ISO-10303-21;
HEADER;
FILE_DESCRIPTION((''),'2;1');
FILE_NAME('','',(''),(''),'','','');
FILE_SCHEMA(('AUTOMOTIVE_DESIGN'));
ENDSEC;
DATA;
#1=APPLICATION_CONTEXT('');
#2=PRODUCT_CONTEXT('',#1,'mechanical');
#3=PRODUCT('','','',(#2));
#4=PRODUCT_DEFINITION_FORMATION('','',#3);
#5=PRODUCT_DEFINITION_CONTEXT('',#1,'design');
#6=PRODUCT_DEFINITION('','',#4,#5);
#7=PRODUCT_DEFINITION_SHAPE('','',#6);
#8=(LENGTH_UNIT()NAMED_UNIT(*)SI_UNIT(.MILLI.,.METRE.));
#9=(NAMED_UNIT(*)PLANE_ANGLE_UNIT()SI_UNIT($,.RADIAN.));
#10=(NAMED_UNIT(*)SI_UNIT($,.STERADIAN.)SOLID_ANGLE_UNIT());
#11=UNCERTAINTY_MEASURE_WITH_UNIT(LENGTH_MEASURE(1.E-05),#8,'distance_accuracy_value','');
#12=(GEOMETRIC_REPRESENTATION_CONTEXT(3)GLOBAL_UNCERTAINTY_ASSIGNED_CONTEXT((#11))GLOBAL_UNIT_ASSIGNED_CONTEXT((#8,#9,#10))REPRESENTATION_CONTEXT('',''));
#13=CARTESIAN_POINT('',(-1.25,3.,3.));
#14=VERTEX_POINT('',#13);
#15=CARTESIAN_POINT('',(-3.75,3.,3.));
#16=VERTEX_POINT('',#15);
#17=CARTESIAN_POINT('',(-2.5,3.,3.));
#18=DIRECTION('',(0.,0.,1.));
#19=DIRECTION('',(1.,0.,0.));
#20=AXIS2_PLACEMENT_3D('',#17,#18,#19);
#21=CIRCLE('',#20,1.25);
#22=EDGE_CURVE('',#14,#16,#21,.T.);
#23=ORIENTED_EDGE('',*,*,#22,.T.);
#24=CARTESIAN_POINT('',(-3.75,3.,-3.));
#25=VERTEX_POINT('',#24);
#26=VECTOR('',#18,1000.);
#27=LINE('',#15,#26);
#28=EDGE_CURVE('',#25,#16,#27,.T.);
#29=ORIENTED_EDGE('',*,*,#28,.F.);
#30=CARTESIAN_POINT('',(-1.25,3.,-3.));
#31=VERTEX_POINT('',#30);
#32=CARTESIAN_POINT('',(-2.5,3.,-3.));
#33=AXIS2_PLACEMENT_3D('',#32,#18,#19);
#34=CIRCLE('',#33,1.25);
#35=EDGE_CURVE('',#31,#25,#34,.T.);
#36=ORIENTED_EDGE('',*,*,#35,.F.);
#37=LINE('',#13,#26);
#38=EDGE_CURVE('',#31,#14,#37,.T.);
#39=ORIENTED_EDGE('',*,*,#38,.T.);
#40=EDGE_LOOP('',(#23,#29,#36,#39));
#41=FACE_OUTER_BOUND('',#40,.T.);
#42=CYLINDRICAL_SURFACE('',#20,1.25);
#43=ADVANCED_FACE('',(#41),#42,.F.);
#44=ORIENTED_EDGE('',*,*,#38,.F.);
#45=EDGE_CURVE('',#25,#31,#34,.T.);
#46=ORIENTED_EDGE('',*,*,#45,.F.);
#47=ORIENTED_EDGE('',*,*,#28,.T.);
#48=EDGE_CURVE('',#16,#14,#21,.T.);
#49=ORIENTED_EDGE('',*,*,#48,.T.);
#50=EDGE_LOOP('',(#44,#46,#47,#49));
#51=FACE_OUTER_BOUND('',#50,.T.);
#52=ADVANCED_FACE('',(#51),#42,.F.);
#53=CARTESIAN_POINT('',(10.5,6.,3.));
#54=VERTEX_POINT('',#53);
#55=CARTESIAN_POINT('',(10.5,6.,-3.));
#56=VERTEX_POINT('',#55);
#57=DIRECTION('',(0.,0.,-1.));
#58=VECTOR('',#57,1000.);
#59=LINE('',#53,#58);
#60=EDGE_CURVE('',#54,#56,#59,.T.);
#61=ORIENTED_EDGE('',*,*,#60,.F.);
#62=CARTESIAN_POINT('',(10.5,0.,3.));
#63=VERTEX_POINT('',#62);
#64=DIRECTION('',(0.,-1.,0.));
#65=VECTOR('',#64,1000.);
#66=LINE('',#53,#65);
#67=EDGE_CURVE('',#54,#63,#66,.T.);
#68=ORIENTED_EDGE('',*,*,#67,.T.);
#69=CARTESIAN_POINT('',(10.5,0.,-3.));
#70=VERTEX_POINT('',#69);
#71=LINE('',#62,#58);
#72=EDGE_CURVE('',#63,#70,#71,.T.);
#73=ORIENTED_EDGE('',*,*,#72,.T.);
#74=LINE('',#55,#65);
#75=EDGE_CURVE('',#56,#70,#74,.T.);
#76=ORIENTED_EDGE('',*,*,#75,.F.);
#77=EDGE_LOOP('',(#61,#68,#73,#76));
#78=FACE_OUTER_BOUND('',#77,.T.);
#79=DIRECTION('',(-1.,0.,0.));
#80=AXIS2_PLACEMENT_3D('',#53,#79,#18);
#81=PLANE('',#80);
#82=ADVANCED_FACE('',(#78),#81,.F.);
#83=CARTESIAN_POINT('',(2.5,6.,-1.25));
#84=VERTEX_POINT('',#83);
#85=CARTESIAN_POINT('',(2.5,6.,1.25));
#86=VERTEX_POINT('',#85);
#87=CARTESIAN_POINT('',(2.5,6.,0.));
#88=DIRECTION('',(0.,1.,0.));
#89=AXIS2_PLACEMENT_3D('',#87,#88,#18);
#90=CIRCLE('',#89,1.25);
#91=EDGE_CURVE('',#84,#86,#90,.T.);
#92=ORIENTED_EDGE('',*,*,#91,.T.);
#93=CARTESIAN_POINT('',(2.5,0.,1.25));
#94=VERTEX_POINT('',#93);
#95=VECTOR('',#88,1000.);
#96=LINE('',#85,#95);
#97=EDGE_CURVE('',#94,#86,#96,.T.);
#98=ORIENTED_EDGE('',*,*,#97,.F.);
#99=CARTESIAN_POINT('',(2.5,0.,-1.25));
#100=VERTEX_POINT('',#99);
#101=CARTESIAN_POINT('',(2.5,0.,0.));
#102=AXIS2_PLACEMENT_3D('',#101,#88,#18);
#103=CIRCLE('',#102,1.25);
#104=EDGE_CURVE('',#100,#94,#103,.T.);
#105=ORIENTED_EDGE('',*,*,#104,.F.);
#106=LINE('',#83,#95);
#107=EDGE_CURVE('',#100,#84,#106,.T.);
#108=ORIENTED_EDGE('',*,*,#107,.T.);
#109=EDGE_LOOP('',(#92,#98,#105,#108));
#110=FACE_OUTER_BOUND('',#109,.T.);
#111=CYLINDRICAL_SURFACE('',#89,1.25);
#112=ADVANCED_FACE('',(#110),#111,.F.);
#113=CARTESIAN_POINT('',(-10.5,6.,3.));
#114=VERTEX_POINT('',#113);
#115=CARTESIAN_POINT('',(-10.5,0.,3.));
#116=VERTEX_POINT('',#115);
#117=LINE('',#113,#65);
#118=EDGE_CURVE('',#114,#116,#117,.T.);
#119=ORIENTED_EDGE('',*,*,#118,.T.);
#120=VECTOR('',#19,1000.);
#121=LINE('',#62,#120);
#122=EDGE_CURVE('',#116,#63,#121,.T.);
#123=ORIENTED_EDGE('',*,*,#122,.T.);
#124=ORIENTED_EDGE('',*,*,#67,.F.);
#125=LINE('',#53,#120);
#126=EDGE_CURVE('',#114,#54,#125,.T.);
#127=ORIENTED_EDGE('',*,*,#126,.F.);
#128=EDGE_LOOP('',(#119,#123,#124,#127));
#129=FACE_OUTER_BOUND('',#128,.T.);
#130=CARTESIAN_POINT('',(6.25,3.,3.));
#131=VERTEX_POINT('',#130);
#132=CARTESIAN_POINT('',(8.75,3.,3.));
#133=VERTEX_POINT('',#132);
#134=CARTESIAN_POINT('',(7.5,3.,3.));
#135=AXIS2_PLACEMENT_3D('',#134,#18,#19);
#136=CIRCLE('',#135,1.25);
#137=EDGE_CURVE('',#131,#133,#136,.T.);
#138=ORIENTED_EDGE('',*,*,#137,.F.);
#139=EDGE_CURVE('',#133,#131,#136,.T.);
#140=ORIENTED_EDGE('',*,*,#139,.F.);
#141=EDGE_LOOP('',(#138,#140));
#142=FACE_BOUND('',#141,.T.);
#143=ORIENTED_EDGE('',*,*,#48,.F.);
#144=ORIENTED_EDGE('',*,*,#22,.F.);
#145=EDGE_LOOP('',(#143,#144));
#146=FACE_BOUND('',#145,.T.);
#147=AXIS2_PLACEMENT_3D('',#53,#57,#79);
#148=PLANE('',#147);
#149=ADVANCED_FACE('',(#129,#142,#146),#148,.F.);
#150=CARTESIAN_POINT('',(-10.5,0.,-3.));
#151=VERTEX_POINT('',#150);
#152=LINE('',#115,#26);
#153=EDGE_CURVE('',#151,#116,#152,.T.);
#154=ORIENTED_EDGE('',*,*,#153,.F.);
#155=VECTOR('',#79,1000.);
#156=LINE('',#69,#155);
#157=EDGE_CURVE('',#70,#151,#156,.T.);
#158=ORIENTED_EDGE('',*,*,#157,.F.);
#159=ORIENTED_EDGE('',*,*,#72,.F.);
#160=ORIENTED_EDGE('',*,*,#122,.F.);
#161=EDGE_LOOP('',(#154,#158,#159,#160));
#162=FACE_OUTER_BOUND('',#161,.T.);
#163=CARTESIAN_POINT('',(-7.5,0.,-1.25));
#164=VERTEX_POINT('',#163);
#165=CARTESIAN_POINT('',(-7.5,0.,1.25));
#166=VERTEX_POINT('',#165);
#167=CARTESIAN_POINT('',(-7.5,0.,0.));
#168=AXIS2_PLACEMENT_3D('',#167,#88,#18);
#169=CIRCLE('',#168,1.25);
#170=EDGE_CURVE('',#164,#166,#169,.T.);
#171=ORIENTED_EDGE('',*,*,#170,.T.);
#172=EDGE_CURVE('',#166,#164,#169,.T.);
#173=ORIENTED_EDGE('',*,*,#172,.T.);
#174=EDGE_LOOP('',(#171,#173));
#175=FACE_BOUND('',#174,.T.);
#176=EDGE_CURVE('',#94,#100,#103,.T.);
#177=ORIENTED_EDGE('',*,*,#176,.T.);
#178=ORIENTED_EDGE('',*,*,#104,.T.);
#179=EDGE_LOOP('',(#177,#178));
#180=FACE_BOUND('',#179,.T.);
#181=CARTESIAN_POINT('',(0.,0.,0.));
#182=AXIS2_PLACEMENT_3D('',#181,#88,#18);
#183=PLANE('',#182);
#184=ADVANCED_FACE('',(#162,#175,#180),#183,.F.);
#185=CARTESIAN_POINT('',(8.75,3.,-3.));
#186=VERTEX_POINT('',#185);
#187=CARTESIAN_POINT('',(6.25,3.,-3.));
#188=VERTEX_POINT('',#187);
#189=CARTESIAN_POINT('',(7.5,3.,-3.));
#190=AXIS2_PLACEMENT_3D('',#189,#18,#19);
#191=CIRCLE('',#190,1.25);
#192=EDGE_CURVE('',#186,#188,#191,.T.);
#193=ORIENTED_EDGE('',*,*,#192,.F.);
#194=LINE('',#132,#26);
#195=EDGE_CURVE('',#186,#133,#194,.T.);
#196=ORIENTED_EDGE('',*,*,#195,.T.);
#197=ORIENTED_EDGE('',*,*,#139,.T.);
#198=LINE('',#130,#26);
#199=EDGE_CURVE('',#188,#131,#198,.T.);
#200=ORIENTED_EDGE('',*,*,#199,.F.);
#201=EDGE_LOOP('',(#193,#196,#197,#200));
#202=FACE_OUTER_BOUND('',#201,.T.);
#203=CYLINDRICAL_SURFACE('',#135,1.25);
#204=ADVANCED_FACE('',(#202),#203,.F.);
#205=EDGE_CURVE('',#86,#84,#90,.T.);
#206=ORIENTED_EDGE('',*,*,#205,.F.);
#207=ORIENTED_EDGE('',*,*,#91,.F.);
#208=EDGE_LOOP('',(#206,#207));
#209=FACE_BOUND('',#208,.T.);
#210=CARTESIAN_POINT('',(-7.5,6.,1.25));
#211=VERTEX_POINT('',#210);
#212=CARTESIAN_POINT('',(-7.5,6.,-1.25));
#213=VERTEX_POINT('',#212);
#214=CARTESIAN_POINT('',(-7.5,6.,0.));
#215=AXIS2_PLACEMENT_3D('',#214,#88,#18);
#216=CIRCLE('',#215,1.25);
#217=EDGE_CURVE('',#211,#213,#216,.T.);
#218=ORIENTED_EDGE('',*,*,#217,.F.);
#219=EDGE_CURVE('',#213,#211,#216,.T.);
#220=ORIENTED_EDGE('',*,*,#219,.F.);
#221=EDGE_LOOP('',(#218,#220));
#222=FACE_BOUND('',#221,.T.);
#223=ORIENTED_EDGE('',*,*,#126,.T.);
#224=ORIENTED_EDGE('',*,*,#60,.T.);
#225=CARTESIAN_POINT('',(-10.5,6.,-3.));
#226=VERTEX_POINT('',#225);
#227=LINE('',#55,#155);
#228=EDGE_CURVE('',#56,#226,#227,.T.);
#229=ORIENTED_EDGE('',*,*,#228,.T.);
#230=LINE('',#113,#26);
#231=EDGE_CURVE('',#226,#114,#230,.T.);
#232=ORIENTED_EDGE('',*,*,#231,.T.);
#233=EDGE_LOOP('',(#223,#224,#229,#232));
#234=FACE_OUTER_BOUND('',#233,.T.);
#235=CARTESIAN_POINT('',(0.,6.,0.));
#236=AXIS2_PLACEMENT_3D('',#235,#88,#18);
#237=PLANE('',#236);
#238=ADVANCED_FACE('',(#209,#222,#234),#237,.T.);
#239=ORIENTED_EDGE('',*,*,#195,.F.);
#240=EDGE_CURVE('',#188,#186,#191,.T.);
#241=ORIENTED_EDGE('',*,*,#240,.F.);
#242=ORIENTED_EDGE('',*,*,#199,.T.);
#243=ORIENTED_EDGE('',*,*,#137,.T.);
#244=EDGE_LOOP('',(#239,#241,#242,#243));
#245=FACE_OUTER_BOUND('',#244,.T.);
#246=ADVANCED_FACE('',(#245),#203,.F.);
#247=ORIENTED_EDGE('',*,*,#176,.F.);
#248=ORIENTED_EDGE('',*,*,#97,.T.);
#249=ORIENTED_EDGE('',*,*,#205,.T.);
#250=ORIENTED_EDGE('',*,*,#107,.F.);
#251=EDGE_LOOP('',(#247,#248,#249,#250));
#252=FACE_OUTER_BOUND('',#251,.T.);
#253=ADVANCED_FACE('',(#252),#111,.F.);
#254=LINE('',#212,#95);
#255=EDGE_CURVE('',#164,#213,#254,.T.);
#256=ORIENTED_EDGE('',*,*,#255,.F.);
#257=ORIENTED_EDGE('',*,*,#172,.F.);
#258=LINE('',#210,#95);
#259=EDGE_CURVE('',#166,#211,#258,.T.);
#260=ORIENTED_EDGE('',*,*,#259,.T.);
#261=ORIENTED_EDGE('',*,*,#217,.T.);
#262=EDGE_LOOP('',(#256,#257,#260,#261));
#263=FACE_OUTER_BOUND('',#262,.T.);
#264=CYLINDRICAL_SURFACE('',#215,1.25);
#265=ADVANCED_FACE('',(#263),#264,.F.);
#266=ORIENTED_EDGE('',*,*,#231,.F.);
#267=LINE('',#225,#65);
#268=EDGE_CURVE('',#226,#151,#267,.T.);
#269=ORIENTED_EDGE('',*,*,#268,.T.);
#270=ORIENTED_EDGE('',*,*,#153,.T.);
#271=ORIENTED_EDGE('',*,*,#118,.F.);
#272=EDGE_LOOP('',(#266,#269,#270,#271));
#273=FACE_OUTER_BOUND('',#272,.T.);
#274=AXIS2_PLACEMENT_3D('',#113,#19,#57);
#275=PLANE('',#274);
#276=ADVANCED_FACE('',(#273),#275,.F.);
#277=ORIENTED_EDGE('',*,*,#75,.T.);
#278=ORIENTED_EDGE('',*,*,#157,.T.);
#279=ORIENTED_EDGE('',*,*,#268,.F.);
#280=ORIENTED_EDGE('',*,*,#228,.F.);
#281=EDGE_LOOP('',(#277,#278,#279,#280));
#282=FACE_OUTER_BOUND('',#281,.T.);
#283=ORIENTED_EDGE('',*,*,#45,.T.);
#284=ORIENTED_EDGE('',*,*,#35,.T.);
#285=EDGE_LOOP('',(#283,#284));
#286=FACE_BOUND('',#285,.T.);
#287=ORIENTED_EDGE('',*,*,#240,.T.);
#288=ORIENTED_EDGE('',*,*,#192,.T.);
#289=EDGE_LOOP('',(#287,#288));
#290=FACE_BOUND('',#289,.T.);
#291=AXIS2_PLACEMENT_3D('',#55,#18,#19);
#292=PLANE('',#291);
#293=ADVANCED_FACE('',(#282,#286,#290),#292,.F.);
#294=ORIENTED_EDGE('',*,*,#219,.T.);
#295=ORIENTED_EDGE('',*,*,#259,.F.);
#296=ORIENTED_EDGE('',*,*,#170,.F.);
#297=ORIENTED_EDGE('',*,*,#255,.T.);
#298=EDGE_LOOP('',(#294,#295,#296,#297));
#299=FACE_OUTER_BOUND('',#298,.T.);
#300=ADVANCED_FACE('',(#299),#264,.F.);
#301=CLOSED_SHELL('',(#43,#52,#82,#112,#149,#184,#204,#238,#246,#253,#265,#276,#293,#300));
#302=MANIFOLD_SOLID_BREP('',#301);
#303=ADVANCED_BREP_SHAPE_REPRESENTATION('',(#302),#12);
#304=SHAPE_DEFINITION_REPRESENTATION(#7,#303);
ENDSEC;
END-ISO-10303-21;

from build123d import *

# Parameters (mm, degrees)
SKETCH_1_W         = 21
SKETCH_1_H         = 6
EXTRUDE_1_DEPTH    = 6
HOLE_WIZARD_M3_1_D = 2.5
HOLE_WIZARD_M3_2_D = 2.5


with BuildPart() as part:
    # 草图1 → 凸台-拉伸1 (new body)
    with BuildSketch(Plane(origin=(0, 0, 0), x_dir=(1, 0, 0), z_dir=(0, 1, 0))):
        Rectangle(SKETCH_1_W, SKETCH_1_H)
    extrude(amount=EXTRUDE_1_DEPTH)

    # M3 螺纹孔1 (through all)
    with Locations(Plane.XY.offset(3)):
        with Locations((-2.5, 3), (7.5, 3)):
            Hole(HOLE_WIZARD_M3_1_D / 2)

    # M3 螺纹孔2 (through all)
    with Locations(Plane(origin=(0, 6, 0), x_dir=(1, 0, 0), z_dir=(0, 1, 0))):
        with Locations((2.5, 0), (-7.5, 0)):
            Hole(HOLE_WIZARD_M3_2_D / 2)


solid = part.part
